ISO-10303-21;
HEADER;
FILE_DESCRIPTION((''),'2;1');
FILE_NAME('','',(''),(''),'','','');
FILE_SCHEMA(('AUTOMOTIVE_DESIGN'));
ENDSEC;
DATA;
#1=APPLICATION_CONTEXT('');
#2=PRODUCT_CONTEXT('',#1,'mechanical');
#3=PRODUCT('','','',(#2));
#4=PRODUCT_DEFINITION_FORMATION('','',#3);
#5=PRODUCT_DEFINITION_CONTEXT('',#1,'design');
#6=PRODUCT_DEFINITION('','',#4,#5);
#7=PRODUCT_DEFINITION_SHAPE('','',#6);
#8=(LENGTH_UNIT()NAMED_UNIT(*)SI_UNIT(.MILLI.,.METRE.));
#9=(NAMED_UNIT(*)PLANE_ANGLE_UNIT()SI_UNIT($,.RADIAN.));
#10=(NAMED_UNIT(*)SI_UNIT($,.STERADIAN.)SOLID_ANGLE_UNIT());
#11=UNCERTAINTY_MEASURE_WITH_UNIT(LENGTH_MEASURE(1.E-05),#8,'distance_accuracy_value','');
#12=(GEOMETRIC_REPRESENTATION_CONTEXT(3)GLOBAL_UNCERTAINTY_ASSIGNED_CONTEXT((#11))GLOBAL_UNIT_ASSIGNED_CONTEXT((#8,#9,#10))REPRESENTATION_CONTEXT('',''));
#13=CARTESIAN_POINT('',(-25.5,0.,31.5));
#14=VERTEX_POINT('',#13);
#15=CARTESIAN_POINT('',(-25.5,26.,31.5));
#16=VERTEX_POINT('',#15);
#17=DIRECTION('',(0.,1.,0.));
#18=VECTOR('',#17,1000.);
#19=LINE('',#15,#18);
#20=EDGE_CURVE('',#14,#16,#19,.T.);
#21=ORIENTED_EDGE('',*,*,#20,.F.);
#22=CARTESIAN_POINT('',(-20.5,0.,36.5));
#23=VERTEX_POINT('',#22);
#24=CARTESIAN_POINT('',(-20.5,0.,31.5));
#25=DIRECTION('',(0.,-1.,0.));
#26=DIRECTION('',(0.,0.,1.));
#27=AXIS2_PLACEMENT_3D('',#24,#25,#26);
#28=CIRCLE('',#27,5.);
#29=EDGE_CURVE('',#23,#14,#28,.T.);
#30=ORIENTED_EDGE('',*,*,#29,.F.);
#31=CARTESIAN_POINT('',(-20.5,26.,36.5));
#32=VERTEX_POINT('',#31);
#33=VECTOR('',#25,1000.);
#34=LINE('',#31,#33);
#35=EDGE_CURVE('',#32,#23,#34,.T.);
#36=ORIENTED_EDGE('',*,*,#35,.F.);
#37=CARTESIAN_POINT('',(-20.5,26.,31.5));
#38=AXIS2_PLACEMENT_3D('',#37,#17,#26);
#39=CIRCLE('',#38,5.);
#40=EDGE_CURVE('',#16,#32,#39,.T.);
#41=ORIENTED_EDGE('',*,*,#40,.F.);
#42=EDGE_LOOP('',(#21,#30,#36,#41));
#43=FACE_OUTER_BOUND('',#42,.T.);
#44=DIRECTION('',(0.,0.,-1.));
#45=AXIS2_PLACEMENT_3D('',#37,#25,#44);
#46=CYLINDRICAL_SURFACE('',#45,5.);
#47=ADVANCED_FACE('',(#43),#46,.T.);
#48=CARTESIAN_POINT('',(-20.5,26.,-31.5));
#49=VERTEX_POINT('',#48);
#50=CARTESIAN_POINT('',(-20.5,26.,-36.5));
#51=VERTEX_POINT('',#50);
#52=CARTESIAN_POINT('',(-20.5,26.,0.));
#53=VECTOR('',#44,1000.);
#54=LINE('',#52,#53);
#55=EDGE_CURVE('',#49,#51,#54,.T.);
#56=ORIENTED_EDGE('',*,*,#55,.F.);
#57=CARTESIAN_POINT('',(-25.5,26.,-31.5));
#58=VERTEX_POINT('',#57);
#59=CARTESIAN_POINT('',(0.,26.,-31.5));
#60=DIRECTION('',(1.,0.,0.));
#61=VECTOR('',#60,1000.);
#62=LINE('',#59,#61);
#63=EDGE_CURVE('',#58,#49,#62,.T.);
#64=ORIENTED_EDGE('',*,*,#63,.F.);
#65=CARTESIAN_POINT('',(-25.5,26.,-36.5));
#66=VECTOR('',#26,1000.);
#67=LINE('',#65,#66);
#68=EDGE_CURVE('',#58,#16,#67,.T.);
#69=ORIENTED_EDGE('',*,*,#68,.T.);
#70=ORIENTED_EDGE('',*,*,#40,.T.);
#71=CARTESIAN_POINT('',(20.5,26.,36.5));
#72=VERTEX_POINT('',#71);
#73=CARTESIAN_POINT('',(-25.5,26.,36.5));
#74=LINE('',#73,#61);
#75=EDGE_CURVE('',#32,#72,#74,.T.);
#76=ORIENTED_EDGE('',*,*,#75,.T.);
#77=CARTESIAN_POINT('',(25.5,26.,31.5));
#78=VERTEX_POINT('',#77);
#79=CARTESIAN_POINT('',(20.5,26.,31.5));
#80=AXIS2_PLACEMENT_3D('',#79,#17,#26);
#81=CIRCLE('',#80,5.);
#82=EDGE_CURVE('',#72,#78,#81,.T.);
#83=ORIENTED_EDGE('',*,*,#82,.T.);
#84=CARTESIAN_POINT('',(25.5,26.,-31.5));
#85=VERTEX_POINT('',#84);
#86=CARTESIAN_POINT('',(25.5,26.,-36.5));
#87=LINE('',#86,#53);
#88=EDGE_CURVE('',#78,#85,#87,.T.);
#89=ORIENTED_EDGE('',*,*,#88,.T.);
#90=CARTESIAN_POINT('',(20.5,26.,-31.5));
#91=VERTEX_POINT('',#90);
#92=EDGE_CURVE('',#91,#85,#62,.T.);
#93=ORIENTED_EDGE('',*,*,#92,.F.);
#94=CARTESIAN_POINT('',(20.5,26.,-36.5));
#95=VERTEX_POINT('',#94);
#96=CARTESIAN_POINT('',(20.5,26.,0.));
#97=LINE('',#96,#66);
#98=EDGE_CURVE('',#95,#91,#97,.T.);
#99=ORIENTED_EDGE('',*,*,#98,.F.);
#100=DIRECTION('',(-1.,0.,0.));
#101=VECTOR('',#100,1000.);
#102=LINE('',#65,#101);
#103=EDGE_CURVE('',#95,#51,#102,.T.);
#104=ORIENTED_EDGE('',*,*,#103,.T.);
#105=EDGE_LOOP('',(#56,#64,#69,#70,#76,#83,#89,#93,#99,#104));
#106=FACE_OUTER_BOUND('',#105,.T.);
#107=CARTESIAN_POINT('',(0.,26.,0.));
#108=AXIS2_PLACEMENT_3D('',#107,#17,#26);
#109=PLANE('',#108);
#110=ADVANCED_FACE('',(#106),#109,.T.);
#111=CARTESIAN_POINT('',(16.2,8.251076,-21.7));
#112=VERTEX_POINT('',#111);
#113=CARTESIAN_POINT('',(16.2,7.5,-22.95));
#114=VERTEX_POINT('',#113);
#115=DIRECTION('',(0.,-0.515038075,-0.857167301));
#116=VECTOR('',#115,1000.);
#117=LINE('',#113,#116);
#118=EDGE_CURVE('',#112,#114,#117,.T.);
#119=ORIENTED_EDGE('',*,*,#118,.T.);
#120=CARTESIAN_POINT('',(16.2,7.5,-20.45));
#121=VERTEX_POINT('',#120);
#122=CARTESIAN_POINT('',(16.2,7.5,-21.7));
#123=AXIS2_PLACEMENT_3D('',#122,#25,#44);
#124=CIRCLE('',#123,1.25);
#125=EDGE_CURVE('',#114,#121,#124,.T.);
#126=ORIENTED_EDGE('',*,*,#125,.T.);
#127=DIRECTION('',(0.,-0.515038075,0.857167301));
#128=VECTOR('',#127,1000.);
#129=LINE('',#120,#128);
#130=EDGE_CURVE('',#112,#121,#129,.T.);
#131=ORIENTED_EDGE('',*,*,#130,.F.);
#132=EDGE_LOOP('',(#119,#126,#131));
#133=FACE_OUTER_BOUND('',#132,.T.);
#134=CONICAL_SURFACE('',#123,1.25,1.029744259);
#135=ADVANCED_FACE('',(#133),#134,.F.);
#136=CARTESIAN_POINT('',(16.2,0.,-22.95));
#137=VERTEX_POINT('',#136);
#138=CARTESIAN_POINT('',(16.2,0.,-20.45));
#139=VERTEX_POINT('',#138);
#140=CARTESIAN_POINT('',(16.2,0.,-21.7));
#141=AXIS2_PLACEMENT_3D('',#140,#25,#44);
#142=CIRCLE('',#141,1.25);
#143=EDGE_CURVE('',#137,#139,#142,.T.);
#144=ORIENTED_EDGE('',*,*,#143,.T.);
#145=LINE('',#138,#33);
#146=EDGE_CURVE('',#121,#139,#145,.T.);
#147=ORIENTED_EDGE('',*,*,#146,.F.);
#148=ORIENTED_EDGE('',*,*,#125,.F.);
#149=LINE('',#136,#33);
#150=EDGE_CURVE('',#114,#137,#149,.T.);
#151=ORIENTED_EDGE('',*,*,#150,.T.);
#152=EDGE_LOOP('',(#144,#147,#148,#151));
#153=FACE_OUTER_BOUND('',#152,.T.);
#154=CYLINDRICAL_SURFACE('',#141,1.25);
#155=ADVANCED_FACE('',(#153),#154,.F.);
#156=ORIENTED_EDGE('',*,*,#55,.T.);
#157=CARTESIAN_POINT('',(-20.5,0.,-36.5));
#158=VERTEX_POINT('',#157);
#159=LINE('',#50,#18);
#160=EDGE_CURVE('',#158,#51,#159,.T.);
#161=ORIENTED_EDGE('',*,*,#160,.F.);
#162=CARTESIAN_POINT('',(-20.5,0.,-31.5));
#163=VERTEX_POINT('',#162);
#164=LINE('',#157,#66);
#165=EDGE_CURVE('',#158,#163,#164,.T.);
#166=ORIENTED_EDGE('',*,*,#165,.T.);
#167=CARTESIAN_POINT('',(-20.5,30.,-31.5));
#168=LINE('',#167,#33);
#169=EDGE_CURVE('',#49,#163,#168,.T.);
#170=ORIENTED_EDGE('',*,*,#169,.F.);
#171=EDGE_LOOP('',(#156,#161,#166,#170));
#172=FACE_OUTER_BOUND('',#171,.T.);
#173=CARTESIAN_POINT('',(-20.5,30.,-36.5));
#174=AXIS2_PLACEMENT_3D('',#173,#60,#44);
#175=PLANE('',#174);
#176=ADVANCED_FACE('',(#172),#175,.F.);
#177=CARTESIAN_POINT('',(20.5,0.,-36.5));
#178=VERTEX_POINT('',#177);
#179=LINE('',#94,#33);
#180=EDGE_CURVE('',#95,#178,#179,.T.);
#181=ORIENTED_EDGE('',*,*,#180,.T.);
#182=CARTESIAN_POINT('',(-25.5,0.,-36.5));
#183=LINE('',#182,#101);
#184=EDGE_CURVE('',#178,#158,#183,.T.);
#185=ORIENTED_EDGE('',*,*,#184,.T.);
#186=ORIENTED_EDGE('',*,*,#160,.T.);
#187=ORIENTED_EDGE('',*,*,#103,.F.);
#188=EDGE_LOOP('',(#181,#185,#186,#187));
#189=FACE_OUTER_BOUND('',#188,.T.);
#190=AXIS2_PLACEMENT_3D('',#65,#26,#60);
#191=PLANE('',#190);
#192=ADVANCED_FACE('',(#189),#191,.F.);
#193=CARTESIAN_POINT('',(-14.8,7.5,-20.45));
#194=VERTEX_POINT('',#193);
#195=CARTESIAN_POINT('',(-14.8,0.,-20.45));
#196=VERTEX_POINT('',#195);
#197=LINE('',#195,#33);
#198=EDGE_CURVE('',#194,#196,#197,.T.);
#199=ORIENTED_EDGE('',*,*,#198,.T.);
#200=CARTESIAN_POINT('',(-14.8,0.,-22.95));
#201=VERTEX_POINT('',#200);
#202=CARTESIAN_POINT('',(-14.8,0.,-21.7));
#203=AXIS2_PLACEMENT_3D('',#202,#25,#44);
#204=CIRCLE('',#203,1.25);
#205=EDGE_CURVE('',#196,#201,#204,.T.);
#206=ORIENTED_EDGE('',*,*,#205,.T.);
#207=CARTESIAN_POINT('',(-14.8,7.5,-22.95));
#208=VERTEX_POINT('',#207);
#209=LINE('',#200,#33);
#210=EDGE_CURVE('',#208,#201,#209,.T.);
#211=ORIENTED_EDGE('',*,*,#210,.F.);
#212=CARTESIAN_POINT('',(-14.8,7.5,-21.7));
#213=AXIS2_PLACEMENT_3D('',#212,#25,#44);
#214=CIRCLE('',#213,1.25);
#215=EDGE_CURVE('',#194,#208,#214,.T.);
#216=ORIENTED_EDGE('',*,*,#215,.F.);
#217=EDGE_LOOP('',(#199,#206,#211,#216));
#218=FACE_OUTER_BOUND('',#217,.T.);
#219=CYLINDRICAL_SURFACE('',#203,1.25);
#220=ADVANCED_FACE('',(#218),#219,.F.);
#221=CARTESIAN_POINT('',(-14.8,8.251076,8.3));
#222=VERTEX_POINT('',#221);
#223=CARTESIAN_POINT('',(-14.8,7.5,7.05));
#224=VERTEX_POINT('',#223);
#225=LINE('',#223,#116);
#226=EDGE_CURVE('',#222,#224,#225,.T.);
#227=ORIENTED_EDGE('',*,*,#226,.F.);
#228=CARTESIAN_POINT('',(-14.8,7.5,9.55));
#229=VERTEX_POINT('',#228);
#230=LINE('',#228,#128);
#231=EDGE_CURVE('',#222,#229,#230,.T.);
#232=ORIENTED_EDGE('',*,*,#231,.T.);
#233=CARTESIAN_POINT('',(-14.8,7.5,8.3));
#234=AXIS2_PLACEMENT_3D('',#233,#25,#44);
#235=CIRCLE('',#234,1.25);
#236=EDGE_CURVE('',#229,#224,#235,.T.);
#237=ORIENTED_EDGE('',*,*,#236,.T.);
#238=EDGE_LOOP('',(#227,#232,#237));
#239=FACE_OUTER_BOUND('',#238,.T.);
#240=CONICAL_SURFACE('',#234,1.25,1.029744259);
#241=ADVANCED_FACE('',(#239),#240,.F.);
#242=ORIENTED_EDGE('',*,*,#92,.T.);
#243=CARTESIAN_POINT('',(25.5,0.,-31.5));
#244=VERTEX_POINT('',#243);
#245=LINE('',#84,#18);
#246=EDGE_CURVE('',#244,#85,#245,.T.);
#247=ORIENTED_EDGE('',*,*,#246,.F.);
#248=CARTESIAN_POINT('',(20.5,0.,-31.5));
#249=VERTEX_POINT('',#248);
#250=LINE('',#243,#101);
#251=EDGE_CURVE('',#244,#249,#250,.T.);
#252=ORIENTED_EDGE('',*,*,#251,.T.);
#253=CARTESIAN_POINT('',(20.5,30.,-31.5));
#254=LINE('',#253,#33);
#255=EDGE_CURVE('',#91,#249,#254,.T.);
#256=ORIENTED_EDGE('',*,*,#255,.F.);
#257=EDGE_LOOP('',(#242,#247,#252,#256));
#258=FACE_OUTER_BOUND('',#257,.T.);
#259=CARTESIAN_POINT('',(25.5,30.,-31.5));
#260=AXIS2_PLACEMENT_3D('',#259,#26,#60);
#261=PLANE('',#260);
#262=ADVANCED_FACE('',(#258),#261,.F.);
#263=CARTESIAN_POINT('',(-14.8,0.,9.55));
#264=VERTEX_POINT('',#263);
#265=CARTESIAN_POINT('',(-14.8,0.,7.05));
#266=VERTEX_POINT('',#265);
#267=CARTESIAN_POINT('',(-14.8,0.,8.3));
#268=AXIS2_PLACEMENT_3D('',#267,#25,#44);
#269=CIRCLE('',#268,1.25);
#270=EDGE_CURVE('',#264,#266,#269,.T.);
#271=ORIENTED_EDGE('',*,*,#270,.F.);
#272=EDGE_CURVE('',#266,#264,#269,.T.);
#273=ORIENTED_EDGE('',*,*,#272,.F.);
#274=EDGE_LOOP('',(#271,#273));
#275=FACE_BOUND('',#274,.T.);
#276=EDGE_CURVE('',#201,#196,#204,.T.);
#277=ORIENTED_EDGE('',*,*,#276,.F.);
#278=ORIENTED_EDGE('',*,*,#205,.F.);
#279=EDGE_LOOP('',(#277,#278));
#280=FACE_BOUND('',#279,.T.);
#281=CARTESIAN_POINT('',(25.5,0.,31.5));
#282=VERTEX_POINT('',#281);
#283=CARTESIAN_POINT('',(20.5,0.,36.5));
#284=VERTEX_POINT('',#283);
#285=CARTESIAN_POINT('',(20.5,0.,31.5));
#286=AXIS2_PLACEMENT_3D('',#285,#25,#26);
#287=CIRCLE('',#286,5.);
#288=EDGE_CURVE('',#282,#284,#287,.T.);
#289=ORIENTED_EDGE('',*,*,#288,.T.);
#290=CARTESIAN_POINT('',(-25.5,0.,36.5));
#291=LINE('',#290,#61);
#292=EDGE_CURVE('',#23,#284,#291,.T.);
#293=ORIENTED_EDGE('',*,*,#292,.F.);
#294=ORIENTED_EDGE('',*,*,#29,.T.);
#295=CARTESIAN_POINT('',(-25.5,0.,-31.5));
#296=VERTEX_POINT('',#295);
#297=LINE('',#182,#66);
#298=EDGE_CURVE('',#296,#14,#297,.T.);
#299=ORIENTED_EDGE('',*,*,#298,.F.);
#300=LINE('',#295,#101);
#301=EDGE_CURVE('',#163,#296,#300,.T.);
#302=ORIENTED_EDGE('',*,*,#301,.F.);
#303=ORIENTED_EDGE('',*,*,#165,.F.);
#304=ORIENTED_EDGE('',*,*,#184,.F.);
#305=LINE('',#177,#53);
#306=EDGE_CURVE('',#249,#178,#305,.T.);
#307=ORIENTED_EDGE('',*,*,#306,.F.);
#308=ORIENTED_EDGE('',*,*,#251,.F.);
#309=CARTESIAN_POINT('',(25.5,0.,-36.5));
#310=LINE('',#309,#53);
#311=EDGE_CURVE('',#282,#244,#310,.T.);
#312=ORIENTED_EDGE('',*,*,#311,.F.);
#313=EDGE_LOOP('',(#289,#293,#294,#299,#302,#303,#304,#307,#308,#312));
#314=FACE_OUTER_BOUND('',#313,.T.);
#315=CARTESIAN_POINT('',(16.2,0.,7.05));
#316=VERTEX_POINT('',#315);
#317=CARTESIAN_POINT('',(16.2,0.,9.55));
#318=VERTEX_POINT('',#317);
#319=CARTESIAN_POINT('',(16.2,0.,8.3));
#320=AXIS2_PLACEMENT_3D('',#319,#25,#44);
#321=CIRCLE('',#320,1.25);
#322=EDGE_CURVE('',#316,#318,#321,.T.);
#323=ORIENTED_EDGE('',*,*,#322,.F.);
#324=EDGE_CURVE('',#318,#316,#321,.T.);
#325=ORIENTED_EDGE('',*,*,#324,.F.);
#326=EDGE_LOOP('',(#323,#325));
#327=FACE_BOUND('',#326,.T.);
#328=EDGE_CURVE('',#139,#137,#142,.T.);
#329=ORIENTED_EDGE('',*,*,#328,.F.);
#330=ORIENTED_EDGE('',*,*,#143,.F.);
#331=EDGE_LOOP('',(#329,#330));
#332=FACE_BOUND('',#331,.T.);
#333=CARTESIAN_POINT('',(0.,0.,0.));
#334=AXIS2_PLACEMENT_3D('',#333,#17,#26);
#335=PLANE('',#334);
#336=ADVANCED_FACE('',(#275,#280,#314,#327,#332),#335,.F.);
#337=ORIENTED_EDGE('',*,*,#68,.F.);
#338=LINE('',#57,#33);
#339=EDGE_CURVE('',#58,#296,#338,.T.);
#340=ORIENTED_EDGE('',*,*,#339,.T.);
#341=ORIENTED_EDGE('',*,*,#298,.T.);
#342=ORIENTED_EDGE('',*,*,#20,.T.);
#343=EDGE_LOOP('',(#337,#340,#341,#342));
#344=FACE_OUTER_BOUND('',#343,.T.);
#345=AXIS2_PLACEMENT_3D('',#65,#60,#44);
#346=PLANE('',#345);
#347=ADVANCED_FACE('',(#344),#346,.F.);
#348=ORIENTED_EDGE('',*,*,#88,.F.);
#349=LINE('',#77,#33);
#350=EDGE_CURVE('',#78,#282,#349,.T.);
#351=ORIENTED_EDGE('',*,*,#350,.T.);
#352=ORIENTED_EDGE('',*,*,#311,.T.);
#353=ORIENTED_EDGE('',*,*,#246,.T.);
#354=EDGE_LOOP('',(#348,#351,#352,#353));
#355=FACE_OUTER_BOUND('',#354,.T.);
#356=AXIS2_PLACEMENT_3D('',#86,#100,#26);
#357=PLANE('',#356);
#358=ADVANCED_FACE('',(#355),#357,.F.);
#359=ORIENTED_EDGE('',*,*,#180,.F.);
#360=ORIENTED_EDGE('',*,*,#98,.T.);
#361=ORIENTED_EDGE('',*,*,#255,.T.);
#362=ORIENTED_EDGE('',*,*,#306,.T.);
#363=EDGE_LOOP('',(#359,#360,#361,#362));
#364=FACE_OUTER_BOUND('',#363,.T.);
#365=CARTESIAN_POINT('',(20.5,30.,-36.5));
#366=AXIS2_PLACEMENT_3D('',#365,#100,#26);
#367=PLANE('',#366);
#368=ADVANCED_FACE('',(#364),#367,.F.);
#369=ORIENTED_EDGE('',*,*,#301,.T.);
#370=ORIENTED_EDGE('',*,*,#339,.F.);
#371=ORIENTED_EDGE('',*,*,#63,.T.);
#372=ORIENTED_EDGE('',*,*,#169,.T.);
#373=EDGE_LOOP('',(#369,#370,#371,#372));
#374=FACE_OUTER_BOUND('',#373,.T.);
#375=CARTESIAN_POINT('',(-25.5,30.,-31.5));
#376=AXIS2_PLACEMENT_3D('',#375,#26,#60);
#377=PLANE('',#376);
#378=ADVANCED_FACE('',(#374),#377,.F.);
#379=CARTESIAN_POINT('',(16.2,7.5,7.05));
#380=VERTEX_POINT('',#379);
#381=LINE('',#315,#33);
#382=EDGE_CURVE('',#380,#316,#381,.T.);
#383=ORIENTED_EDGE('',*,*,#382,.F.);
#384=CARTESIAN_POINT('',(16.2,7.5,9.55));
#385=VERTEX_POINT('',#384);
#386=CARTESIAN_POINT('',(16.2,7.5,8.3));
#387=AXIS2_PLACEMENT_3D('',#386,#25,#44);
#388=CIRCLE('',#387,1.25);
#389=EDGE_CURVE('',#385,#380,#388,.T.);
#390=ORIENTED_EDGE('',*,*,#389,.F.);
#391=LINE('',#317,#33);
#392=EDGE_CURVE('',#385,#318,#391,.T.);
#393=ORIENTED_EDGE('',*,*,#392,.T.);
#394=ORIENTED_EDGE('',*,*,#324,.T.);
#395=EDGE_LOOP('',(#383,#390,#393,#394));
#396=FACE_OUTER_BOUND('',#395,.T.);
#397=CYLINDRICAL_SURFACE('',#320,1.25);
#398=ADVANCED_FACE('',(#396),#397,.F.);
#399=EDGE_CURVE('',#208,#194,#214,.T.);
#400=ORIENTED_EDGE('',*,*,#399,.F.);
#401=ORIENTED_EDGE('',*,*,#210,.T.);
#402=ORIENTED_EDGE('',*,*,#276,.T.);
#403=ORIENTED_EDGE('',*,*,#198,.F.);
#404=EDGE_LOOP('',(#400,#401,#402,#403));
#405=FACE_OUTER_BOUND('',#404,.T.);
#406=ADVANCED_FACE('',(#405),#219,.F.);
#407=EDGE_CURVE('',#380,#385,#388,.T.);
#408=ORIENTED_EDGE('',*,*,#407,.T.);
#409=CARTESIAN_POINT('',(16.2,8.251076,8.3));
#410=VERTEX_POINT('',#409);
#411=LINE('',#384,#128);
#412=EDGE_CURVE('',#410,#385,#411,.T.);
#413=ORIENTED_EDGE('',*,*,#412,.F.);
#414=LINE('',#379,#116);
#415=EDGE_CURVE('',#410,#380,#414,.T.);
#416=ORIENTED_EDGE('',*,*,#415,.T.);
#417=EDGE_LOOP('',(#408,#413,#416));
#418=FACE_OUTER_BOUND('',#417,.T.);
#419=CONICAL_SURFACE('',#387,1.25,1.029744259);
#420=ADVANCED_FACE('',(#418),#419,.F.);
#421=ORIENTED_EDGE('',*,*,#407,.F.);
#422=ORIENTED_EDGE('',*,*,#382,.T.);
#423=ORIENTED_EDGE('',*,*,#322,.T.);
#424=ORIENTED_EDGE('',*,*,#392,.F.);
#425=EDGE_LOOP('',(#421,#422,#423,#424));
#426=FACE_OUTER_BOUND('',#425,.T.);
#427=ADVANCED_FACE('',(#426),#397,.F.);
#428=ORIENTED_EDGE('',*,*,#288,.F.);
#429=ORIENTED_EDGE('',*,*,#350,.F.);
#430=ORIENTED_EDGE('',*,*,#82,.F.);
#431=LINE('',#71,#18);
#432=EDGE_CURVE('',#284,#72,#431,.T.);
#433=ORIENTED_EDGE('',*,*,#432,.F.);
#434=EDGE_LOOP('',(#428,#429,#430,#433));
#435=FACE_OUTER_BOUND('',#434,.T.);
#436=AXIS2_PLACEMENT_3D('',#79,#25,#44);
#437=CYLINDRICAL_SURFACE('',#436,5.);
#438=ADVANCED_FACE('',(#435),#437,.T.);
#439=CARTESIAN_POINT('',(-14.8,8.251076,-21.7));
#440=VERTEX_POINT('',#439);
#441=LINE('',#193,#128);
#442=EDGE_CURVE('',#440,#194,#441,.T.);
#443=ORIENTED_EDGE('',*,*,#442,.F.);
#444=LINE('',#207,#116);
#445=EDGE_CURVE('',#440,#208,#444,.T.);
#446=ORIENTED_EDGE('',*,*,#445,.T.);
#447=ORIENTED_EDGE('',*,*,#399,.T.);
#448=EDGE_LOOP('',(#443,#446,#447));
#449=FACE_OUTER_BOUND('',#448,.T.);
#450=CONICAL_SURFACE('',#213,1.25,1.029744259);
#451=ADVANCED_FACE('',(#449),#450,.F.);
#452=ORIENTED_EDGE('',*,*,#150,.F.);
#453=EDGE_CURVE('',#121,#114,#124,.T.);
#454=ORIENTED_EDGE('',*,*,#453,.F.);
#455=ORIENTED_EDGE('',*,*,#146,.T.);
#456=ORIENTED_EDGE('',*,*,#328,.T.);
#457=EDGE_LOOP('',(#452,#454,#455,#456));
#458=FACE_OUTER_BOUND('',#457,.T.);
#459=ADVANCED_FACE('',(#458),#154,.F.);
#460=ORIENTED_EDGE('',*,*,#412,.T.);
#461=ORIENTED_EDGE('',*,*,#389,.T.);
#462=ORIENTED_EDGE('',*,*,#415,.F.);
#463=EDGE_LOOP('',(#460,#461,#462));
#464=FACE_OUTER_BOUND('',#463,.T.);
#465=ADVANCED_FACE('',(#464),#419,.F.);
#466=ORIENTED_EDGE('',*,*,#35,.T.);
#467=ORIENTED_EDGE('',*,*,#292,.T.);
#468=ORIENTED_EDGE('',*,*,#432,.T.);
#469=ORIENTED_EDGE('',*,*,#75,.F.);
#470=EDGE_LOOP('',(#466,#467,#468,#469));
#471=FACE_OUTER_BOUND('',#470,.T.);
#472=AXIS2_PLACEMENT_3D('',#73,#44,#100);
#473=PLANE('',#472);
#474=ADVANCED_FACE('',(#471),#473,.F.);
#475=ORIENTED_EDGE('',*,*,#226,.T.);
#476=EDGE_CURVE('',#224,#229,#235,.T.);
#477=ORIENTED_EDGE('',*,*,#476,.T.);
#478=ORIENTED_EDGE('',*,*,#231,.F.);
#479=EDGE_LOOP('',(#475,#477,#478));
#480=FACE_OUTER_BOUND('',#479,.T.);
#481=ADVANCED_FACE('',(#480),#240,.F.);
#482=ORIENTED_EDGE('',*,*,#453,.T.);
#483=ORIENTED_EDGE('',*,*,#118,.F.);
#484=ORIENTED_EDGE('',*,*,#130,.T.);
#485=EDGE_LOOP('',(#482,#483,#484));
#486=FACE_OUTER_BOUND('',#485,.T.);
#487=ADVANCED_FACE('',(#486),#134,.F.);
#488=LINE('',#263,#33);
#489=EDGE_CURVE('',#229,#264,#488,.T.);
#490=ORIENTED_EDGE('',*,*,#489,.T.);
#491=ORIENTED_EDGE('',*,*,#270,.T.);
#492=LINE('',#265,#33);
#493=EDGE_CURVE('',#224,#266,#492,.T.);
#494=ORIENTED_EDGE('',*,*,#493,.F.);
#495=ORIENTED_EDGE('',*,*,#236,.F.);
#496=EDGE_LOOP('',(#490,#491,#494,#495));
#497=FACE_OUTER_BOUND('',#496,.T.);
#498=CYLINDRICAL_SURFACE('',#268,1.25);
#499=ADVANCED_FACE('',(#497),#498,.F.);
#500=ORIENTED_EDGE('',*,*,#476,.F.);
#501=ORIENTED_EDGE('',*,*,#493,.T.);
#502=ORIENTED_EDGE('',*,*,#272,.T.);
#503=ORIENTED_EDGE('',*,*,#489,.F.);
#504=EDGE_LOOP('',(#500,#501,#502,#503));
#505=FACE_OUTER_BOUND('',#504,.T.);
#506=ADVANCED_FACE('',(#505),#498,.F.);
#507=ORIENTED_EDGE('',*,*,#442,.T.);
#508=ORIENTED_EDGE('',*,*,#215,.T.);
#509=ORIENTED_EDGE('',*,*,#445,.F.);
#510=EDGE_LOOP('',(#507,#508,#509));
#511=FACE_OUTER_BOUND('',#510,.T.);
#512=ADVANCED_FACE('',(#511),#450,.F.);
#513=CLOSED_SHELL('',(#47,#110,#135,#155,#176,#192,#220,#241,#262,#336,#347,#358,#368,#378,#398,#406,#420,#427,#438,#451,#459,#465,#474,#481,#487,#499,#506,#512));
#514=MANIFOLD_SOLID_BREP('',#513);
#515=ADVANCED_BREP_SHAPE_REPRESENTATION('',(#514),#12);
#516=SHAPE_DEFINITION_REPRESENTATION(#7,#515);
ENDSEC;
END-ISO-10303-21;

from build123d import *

# Parameters (mm, degrees)
SKETCH_1_W             = 51
SKETCH_1_H             = 73
EXTRUDE_1_DEPTH        = 26
FILLET_1_R             = 5
SKETCH_2_W             = 5
SKETCH_2_H             = 5
CUT_EXTRUDE_1_DEPTH    = 30
HOLE_WIZARD_M3_1_D     = 2.5
HOLE_WIZARD_M3_1_DEPTH = 7.5
HOLE_WIZARD_M3_1_TIP   = 0.751075774


with BuildPart() as part:
    # 草图1 → 凸台-拉伸1 (new body)
    with BuildSketch(Plane(origin=(0, 0, 0), x_dir=(1, 0, 0), z_dir=(0, 1, 0))):
        Rectangle(SKETCH_1_W, SKETCH_1_H)
    extrude(amount=EXTRUDE_1_DEPTH)

    # 圆角1
    fillet_1_edges = [part.edges().sort_by_distance(p)[0] for p in [
        (25.5, 13, 36.5),
        (-25.5, 13, 36.5),
        (-25.5, 13, -36.5),
        (25.5, 13, -36.5),
    ]]
    fillet(fillet_1_edges, radius=FILLET_1_R)

    # 草图2 → 切除-拉伸1 (cut)
    with BuildSketch(Plane.XZ):
        with Locations((23, -34)):
            Rectangle(SKETCH_2_W, SKETCH_2_H)
        with Locations((-23, -34)):
            Rectangle(SKETCH_2_W, SKETCH_2_H)
    extrude(amount=-CUT_EXTRUDE_1_DEPTH, mode=Mode.SUBTRACT)

    # M3 螺纹孔1
    with Locations(Plane(origin=(0, 0, 0), x_dir=(-1, 0, 0), z_dir=(0, -1, 0))):
        with Locations((14.8, -8.3), (-16.2, -8.3), (14.8, 21.7), (-16.2, 21.7)):
            Hole(HOLE_WIZARD_M3_1_D / 2, depth=HOLE_WIZARD_M3_1_DEPTH)
            with Locations((0, 0, -(HOLE_WIZARD_M3_1_DEPTH + HOLE_WIZARD_M3_1_TIP / 2))):  # 118° drill point
                Cone(0, HOLE_WIZARD_M3_1_D / 2, HOLE_WIZARD_M3_1_TIP, mode=Mode.SUBTRACT)


solid = part.part
